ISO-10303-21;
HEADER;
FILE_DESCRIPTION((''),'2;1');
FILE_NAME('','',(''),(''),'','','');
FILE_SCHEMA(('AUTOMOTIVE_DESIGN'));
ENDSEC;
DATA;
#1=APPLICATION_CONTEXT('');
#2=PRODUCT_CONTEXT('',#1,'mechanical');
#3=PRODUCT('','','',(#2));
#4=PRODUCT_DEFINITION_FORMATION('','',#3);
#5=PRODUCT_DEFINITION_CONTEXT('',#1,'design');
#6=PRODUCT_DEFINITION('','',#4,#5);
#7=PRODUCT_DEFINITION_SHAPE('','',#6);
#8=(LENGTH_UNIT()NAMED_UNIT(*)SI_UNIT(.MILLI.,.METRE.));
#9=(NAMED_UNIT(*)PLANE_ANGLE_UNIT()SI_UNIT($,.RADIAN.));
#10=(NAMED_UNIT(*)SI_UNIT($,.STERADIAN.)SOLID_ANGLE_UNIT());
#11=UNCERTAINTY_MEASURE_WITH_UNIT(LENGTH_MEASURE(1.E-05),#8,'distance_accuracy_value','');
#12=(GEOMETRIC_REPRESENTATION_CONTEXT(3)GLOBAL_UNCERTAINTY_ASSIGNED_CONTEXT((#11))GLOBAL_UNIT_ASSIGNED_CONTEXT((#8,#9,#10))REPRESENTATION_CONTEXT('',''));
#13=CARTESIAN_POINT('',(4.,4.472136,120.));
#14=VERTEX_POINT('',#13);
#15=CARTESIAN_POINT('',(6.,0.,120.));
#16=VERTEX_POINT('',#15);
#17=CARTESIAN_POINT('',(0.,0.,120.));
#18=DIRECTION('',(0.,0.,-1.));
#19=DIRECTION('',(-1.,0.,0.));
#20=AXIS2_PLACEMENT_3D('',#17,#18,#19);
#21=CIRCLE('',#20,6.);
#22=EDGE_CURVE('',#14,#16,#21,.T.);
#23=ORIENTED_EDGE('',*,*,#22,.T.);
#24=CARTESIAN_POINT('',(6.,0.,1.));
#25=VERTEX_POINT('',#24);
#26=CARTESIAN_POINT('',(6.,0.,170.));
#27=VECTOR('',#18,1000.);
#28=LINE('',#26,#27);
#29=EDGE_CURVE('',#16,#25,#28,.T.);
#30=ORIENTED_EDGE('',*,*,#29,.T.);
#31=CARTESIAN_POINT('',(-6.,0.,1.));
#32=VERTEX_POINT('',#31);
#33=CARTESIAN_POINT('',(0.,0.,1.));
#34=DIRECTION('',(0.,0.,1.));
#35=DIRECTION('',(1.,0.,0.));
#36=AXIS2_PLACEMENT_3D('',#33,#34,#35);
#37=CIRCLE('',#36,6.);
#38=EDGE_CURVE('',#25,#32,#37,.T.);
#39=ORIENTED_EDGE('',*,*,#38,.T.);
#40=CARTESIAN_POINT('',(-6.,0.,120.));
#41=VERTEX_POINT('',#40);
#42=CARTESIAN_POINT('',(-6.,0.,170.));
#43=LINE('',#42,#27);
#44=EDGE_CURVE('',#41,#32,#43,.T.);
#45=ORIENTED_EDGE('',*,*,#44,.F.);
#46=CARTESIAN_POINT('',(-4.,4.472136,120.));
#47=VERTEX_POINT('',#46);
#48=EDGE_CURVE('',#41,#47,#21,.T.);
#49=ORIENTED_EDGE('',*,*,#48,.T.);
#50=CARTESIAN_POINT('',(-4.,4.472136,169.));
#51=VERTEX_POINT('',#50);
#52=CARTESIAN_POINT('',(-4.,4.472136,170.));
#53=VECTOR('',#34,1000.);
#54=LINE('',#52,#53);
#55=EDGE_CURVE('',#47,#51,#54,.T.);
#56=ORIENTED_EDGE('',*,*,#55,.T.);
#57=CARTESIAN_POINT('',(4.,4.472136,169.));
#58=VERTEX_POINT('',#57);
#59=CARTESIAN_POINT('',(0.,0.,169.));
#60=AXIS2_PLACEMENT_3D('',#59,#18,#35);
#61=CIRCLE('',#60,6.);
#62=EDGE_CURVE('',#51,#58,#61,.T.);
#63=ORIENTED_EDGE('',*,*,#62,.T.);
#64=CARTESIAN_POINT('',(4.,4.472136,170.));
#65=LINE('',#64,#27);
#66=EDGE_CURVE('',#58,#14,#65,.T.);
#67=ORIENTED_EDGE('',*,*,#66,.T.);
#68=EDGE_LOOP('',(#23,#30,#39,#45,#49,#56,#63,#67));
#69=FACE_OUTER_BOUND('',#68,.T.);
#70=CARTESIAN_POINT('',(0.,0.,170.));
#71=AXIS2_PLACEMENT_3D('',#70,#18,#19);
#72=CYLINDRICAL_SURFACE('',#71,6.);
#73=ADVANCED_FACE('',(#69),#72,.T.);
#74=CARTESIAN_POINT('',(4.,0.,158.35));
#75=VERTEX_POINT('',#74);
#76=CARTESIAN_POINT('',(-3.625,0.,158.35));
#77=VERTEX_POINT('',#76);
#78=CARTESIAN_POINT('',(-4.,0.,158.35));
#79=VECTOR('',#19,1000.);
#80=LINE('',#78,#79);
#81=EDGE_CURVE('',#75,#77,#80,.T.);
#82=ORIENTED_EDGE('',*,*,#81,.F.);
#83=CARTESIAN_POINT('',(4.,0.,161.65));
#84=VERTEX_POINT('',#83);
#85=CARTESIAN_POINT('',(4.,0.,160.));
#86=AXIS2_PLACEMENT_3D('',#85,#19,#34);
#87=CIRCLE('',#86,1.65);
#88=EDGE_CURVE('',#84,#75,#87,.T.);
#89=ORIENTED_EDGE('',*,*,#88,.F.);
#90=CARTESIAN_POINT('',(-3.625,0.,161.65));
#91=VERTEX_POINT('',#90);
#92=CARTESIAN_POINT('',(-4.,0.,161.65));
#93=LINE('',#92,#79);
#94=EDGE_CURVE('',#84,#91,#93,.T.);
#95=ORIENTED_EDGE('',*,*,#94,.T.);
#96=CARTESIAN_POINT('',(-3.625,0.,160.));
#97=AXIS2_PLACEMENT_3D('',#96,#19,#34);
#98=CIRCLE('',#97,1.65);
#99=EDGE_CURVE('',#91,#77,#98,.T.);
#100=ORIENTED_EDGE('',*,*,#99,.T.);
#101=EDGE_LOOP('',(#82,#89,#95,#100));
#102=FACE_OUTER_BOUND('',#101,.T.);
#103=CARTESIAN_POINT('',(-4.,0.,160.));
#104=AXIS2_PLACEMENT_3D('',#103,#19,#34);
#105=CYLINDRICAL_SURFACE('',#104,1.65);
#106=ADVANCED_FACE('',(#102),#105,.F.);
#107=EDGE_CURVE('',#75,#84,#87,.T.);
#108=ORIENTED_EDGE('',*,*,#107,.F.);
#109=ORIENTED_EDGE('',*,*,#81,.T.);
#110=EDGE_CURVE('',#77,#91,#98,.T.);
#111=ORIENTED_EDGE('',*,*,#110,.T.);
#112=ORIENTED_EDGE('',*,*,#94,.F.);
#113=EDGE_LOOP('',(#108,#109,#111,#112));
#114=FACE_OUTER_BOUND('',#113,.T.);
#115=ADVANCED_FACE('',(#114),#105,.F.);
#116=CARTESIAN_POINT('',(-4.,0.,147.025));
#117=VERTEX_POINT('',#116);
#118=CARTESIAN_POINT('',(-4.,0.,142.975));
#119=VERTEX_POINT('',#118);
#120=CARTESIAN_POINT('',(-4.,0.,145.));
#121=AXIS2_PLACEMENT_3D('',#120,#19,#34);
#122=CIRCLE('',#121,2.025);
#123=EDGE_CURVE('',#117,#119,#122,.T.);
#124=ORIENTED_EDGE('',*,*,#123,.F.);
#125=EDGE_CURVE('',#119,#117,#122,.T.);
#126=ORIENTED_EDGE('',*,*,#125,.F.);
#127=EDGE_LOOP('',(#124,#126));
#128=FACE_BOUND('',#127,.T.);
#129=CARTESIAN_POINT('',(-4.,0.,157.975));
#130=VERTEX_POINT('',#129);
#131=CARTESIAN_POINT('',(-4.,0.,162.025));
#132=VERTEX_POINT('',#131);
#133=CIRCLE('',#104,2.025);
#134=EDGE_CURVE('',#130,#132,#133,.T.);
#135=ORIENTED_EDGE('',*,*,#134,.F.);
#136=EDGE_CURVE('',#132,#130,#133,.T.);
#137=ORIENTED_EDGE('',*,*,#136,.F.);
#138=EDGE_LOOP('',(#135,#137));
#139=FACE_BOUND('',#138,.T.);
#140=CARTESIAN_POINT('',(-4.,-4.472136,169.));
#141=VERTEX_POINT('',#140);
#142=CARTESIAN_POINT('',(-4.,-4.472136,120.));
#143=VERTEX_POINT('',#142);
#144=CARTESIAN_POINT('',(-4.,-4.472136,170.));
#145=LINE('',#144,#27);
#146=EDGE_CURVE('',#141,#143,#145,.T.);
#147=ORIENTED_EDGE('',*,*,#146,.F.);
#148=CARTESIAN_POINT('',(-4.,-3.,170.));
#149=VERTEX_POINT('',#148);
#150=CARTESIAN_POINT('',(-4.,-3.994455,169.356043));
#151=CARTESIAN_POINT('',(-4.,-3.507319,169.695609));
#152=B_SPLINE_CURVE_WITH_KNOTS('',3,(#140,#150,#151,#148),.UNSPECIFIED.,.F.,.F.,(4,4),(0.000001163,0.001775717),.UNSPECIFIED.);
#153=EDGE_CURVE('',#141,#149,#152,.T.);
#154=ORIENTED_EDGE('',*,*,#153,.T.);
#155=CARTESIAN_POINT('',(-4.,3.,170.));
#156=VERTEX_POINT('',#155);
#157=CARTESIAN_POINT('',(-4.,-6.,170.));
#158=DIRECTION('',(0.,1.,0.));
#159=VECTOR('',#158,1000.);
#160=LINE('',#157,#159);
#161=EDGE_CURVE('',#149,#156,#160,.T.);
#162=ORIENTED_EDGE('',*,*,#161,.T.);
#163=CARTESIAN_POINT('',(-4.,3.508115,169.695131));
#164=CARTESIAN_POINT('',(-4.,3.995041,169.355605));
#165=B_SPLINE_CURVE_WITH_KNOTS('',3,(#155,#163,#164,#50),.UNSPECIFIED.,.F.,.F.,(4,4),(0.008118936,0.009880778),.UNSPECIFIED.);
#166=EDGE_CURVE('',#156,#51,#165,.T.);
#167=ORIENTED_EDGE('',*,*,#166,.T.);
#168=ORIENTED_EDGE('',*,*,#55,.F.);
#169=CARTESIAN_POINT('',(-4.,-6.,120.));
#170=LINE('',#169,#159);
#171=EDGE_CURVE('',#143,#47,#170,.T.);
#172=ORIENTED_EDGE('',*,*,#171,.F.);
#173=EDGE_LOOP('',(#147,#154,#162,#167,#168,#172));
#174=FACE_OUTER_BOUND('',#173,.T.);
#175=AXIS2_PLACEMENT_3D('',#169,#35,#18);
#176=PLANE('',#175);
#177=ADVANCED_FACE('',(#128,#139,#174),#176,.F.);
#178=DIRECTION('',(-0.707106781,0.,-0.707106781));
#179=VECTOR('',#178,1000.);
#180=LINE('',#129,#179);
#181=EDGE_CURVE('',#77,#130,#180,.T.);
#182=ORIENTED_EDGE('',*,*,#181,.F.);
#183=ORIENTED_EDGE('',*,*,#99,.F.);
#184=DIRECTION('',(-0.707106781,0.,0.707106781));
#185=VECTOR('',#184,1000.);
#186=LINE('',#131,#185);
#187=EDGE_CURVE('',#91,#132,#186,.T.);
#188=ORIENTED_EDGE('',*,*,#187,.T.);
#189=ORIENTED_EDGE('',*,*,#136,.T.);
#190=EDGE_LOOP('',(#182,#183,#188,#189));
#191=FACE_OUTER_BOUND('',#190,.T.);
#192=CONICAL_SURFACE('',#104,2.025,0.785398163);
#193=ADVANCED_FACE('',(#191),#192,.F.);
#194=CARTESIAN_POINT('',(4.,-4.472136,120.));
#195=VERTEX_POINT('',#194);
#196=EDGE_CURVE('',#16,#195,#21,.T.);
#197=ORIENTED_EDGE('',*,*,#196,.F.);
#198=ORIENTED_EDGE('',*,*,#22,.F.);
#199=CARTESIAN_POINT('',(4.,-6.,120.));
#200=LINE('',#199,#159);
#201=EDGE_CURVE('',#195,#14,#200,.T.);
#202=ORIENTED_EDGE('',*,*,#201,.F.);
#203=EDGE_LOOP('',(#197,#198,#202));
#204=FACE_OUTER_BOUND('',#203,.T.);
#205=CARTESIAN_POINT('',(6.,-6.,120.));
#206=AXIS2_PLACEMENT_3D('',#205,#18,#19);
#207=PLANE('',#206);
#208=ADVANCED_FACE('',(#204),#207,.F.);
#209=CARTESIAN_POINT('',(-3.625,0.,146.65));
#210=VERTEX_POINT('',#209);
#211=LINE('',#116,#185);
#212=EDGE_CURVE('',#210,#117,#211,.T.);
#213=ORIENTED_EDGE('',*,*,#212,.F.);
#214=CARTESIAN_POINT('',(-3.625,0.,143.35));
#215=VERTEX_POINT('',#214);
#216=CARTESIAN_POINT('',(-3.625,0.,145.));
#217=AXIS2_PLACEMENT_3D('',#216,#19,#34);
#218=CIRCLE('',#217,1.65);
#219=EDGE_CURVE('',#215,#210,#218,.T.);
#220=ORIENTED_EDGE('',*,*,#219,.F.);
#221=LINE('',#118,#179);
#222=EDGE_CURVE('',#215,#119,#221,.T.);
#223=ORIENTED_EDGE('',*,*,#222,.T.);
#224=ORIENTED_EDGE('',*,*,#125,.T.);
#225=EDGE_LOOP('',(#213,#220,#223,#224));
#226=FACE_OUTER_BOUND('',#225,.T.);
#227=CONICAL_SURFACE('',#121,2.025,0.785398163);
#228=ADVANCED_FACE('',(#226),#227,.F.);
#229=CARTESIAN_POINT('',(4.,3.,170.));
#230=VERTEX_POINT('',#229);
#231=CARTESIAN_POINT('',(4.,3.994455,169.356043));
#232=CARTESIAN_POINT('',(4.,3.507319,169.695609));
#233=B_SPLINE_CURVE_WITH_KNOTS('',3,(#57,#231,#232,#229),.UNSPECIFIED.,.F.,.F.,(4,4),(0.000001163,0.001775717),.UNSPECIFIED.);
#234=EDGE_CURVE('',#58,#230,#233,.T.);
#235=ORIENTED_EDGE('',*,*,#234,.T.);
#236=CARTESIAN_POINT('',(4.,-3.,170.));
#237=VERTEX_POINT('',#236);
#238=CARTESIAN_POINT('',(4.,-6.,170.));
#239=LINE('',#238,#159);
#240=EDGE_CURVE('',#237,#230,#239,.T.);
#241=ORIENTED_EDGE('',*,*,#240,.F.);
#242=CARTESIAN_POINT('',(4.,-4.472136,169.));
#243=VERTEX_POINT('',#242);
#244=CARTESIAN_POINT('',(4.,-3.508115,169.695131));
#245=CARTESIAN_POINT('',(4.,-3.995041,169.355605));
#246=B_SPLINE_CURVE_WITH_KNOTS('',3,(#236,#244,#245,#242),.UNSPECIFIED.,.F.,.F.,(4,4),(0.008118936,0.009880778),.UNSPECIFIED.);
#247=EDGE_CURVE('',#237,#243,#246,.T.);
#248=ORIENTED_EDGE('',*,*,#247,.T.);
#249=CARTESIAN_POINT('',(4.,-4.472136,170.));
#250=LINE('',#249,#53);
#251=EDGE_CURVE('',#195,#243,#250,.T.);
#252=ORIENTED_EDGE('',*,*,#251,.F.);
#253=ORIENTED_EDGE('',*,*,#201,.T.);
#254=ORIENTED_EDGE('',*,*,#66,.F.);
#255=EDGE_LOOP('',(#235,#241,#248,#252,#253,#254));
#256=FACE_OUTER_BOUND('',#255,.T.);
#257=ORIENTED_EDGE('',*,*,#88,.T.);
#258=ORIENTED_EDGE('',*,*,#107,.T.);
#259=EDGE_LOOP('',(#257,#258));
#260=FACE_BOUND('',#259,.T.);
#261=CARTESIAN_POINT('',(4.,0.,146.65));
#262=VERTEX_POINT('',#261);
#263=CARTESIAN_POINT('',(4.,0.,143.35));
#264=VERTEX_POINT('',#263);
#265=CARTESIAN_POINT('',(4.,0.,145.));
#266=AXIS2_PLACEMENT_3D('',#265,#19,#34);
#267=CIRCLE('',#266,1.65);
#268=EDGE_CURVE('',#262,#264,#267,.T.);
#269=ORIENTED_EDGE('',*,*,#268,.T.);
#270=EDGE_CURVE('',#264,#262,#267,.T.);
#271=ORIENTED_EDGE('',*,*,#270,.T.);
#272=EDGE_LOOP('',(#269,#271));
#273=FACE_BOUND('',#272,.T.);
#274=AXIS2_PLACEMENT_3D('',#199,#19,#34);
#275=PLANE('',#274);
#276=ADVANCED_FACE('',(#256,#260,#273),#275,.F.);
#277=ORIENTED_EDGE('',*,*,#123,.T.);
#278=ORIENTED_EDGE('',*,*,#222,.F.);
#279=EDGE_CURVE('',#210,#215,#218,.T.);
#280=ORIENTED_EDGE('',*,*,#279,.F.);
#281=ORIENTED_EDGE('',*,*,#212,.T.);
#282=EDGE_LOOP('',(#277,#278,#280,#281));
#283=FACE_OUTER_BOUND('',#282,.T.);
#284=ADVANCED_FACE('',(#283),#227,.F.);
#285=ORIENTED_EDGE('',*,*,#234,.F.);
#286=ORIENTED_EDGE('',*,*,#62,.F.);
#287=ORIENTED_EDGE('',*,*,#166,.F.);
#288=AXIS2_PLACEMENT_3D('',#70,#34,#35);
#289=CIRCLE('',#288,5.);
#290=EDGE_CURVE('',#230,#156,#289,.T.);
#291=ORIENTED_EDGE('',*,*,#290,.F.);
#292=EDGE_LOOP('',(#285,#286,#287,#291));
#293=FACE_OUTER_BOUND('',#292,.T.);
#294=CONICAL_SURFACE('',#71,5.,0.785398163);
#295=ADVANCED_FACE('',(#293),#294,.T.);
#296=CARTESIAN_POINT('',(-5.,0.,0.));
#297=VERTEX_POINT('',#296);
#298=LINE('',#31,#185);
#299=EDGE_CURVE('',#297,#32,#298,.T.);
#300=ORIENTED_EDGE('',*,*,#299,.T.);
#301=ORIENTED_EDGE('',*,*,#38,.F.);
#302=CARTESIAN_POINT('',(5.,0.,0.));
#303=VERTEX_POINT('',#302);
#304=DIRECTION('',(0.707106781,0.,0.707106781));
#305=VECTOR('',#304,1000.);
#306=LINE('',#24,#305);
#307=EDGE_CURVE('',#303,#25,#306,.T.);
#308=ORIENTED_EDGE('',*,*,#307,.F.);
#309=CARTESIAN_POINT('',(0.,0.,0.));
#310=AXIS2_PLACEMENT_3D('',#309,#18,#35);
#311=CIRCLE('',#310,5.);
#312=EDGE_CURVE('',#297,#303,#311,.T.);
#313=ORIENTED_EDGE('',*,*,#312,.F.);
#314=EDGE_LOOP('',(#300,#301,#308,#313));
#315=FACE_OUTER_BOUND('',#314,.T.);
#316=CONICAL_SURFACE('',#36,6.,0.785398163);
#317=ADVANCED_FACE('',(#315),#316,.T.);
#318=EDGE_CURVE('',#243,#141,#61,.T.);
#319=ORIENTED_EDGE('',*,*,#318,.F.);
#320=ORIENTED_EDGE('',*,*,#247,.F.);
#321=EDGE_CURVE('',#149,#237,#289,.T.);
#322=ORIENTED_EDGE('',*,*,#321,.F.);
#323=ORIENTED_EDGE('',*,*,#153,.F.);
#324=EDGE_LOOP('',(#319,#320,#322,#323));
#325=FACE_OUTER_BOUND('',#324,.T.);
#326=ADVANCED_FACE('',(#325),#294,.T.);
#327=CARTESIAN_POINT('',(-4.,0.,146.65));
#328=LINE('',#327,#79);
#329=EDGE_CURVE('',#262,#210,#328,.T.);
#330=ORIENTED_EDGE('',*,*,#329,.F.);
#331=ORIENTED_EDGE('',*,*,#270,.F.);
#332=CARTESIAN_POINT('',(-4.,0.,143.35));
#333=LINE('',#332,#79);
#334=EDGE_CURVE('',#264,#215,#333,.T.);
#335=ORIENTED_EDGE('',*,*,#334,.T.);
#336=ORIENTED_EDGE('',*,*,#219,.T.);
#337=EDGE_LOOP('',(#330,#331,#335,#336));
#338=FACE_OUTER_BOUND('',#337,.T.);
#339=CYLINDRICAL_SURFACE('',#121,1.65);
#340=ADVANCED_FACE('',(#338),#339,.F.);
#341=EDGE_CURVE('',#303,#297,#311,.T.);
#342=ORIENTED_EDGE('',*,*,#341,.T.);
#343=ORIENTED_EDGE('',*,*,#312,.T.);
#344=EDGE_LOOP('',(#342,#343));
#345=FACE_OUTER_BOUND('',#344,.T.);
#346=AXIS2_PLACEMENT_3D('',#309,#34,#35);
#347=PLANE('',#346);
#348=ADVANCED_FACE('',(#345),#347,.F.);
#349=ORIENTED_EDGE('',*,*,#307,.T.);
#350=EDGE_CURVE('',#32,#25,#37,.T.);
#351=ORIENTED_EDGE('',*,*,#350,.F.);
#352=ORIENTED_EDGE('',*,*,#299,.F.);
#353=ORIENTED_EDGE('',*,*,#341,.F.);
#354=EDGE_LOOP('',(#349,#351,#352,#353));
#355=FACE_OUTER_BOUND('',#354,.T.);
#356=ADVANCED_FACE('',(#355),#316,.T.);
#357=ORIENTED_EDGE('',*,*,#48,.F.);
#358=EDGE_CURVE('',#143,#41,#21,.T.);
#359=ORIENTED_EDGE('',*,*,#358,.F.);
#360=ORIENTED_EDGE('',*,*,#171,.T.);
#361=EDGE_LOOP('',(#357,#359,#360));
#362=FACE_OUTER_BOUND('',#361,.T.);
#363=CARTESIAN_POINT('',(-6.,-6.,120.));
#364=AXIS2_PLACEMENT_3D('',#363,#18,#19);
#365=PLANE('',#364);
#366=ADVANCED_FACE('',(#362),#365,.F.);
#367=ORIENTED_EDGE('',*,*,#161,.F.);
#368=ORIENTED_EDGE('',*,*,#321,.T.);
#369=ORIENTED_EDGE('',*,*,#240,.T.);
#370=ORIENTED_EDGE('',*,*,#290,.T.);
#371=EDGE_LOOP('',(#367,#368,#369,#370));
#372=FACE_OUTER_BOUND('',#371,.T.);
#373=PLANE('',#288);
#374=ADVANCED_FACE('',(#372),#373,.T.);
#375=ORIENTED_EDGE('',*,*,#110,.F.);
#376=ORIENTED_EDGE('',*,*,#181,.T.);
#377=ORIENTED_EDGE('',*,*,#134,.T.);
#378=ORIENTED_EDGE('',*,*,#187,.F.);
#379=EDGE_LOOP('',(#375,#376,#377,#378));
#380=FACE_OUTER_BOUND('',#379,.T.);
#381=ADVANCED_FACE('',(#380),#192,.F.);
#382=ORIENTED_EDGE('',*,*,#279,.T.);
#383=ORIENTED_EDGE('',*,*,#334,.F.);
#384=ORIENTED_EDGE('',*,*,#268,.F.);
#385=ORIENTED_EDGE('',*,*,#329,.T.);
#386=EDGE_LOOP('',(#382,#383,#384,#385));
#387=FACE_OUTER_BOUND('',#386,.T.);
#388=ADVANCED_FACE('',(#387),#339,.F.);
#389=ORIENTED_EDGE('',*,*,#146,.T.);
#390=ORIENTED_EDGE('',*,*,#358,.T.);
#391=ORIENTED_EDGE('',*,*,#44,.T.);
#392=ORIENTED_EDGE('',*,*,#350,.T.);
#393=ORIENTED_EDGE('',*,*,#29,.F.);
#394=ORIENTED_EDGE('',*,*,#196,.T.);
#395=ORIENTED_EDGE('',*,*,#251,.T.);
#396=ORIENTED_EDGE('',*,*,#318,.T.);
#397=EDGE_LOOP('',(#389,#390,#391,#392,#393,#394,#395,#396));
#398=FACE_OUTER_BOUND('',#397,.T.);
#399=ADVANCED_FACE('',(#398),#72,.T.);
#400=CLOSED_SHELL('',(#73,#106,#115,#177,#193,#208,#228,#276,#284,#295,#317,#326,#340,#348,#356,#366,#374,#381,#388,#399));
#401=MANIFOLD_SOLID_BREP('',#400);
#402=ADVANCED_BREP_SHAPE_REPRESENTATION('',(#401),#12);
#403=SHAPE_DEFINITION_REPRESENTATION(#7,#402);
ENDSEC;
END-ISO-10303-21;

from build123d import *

# Parameters (mm, degrees)
SKETCH1_R                   = 6
BOSS_EXTRUDE1_DEPTH         = 170
CHAMFER1_SIZE               = 1
CUT_EXTRUDE1_DEPTH          = 171.211632975
CUT_EXTRUDE1_DEPTH_BACK     = 171.211632975
SKETCH2_W                   = 2
SKETCH2_H                   = 50
M4_TAPPED_HOLE1_D           = 3.3
M4_TAPPED_HOLE1_CSINK_D     = 4.05
M4_TAPPED_HOLE1_CSINK_ANGLE = 90


with BuildPart() as part:
    # Sketch1 → Boss-Extrude1 (new body)
    with BuildSketch(Plane.XY):
        Circle(SKETCH1_R)
    extrude(amount=BOSS_EXTRUDE1_DEPTH)

    # Chamfer1
    chamfer1_edges = [part.edges().sort_by_distance(p)[0] for p in [
        (-6, 0, 0),
        (-6, 0, 170),
    ]]
    chamfer(chamfer1_edges, length=CHAMFER1_SIZE)

    # Sketch2 → Cut-Extrude1 (cut, two sides: drawn at the far end of the back side and taken through both)
    with BuildSketch(Plane(origin=(0, 0, 0), x_dir=(1, 0, 0), z_dir=(0, 1, 0)).offset(-CUT_EXTRUDE1_DEPTH_BACK)):
        with Locations((-5, -145)):
            Rectangle(SKETCH2_W, SKETCH2_H)
        with Locations((5, -145)):
            Rectangle(SKETCH2_W, SKETCH2_H)
    extrude(amount=CUT_EXTRUDE1_DEPTH + CUT_EXTRUDE1_DEPTH_BACK, mode=Mode.SUBTRACT)

    # M4 Tapped Hole1 (through all)
    with Locations(Plane.ZY.offset(4)):
        with Locations((160, 0), (145, 0)):
            CounterSinkHole(M4_TAPPED_HOLE1_D / 2, M4_TAPPED_HOLE1_CSINK_D / 2, counter_sink_angle=M4_TAPPED_HOLE1_CSINK_ANGLE)


solid = part.part
